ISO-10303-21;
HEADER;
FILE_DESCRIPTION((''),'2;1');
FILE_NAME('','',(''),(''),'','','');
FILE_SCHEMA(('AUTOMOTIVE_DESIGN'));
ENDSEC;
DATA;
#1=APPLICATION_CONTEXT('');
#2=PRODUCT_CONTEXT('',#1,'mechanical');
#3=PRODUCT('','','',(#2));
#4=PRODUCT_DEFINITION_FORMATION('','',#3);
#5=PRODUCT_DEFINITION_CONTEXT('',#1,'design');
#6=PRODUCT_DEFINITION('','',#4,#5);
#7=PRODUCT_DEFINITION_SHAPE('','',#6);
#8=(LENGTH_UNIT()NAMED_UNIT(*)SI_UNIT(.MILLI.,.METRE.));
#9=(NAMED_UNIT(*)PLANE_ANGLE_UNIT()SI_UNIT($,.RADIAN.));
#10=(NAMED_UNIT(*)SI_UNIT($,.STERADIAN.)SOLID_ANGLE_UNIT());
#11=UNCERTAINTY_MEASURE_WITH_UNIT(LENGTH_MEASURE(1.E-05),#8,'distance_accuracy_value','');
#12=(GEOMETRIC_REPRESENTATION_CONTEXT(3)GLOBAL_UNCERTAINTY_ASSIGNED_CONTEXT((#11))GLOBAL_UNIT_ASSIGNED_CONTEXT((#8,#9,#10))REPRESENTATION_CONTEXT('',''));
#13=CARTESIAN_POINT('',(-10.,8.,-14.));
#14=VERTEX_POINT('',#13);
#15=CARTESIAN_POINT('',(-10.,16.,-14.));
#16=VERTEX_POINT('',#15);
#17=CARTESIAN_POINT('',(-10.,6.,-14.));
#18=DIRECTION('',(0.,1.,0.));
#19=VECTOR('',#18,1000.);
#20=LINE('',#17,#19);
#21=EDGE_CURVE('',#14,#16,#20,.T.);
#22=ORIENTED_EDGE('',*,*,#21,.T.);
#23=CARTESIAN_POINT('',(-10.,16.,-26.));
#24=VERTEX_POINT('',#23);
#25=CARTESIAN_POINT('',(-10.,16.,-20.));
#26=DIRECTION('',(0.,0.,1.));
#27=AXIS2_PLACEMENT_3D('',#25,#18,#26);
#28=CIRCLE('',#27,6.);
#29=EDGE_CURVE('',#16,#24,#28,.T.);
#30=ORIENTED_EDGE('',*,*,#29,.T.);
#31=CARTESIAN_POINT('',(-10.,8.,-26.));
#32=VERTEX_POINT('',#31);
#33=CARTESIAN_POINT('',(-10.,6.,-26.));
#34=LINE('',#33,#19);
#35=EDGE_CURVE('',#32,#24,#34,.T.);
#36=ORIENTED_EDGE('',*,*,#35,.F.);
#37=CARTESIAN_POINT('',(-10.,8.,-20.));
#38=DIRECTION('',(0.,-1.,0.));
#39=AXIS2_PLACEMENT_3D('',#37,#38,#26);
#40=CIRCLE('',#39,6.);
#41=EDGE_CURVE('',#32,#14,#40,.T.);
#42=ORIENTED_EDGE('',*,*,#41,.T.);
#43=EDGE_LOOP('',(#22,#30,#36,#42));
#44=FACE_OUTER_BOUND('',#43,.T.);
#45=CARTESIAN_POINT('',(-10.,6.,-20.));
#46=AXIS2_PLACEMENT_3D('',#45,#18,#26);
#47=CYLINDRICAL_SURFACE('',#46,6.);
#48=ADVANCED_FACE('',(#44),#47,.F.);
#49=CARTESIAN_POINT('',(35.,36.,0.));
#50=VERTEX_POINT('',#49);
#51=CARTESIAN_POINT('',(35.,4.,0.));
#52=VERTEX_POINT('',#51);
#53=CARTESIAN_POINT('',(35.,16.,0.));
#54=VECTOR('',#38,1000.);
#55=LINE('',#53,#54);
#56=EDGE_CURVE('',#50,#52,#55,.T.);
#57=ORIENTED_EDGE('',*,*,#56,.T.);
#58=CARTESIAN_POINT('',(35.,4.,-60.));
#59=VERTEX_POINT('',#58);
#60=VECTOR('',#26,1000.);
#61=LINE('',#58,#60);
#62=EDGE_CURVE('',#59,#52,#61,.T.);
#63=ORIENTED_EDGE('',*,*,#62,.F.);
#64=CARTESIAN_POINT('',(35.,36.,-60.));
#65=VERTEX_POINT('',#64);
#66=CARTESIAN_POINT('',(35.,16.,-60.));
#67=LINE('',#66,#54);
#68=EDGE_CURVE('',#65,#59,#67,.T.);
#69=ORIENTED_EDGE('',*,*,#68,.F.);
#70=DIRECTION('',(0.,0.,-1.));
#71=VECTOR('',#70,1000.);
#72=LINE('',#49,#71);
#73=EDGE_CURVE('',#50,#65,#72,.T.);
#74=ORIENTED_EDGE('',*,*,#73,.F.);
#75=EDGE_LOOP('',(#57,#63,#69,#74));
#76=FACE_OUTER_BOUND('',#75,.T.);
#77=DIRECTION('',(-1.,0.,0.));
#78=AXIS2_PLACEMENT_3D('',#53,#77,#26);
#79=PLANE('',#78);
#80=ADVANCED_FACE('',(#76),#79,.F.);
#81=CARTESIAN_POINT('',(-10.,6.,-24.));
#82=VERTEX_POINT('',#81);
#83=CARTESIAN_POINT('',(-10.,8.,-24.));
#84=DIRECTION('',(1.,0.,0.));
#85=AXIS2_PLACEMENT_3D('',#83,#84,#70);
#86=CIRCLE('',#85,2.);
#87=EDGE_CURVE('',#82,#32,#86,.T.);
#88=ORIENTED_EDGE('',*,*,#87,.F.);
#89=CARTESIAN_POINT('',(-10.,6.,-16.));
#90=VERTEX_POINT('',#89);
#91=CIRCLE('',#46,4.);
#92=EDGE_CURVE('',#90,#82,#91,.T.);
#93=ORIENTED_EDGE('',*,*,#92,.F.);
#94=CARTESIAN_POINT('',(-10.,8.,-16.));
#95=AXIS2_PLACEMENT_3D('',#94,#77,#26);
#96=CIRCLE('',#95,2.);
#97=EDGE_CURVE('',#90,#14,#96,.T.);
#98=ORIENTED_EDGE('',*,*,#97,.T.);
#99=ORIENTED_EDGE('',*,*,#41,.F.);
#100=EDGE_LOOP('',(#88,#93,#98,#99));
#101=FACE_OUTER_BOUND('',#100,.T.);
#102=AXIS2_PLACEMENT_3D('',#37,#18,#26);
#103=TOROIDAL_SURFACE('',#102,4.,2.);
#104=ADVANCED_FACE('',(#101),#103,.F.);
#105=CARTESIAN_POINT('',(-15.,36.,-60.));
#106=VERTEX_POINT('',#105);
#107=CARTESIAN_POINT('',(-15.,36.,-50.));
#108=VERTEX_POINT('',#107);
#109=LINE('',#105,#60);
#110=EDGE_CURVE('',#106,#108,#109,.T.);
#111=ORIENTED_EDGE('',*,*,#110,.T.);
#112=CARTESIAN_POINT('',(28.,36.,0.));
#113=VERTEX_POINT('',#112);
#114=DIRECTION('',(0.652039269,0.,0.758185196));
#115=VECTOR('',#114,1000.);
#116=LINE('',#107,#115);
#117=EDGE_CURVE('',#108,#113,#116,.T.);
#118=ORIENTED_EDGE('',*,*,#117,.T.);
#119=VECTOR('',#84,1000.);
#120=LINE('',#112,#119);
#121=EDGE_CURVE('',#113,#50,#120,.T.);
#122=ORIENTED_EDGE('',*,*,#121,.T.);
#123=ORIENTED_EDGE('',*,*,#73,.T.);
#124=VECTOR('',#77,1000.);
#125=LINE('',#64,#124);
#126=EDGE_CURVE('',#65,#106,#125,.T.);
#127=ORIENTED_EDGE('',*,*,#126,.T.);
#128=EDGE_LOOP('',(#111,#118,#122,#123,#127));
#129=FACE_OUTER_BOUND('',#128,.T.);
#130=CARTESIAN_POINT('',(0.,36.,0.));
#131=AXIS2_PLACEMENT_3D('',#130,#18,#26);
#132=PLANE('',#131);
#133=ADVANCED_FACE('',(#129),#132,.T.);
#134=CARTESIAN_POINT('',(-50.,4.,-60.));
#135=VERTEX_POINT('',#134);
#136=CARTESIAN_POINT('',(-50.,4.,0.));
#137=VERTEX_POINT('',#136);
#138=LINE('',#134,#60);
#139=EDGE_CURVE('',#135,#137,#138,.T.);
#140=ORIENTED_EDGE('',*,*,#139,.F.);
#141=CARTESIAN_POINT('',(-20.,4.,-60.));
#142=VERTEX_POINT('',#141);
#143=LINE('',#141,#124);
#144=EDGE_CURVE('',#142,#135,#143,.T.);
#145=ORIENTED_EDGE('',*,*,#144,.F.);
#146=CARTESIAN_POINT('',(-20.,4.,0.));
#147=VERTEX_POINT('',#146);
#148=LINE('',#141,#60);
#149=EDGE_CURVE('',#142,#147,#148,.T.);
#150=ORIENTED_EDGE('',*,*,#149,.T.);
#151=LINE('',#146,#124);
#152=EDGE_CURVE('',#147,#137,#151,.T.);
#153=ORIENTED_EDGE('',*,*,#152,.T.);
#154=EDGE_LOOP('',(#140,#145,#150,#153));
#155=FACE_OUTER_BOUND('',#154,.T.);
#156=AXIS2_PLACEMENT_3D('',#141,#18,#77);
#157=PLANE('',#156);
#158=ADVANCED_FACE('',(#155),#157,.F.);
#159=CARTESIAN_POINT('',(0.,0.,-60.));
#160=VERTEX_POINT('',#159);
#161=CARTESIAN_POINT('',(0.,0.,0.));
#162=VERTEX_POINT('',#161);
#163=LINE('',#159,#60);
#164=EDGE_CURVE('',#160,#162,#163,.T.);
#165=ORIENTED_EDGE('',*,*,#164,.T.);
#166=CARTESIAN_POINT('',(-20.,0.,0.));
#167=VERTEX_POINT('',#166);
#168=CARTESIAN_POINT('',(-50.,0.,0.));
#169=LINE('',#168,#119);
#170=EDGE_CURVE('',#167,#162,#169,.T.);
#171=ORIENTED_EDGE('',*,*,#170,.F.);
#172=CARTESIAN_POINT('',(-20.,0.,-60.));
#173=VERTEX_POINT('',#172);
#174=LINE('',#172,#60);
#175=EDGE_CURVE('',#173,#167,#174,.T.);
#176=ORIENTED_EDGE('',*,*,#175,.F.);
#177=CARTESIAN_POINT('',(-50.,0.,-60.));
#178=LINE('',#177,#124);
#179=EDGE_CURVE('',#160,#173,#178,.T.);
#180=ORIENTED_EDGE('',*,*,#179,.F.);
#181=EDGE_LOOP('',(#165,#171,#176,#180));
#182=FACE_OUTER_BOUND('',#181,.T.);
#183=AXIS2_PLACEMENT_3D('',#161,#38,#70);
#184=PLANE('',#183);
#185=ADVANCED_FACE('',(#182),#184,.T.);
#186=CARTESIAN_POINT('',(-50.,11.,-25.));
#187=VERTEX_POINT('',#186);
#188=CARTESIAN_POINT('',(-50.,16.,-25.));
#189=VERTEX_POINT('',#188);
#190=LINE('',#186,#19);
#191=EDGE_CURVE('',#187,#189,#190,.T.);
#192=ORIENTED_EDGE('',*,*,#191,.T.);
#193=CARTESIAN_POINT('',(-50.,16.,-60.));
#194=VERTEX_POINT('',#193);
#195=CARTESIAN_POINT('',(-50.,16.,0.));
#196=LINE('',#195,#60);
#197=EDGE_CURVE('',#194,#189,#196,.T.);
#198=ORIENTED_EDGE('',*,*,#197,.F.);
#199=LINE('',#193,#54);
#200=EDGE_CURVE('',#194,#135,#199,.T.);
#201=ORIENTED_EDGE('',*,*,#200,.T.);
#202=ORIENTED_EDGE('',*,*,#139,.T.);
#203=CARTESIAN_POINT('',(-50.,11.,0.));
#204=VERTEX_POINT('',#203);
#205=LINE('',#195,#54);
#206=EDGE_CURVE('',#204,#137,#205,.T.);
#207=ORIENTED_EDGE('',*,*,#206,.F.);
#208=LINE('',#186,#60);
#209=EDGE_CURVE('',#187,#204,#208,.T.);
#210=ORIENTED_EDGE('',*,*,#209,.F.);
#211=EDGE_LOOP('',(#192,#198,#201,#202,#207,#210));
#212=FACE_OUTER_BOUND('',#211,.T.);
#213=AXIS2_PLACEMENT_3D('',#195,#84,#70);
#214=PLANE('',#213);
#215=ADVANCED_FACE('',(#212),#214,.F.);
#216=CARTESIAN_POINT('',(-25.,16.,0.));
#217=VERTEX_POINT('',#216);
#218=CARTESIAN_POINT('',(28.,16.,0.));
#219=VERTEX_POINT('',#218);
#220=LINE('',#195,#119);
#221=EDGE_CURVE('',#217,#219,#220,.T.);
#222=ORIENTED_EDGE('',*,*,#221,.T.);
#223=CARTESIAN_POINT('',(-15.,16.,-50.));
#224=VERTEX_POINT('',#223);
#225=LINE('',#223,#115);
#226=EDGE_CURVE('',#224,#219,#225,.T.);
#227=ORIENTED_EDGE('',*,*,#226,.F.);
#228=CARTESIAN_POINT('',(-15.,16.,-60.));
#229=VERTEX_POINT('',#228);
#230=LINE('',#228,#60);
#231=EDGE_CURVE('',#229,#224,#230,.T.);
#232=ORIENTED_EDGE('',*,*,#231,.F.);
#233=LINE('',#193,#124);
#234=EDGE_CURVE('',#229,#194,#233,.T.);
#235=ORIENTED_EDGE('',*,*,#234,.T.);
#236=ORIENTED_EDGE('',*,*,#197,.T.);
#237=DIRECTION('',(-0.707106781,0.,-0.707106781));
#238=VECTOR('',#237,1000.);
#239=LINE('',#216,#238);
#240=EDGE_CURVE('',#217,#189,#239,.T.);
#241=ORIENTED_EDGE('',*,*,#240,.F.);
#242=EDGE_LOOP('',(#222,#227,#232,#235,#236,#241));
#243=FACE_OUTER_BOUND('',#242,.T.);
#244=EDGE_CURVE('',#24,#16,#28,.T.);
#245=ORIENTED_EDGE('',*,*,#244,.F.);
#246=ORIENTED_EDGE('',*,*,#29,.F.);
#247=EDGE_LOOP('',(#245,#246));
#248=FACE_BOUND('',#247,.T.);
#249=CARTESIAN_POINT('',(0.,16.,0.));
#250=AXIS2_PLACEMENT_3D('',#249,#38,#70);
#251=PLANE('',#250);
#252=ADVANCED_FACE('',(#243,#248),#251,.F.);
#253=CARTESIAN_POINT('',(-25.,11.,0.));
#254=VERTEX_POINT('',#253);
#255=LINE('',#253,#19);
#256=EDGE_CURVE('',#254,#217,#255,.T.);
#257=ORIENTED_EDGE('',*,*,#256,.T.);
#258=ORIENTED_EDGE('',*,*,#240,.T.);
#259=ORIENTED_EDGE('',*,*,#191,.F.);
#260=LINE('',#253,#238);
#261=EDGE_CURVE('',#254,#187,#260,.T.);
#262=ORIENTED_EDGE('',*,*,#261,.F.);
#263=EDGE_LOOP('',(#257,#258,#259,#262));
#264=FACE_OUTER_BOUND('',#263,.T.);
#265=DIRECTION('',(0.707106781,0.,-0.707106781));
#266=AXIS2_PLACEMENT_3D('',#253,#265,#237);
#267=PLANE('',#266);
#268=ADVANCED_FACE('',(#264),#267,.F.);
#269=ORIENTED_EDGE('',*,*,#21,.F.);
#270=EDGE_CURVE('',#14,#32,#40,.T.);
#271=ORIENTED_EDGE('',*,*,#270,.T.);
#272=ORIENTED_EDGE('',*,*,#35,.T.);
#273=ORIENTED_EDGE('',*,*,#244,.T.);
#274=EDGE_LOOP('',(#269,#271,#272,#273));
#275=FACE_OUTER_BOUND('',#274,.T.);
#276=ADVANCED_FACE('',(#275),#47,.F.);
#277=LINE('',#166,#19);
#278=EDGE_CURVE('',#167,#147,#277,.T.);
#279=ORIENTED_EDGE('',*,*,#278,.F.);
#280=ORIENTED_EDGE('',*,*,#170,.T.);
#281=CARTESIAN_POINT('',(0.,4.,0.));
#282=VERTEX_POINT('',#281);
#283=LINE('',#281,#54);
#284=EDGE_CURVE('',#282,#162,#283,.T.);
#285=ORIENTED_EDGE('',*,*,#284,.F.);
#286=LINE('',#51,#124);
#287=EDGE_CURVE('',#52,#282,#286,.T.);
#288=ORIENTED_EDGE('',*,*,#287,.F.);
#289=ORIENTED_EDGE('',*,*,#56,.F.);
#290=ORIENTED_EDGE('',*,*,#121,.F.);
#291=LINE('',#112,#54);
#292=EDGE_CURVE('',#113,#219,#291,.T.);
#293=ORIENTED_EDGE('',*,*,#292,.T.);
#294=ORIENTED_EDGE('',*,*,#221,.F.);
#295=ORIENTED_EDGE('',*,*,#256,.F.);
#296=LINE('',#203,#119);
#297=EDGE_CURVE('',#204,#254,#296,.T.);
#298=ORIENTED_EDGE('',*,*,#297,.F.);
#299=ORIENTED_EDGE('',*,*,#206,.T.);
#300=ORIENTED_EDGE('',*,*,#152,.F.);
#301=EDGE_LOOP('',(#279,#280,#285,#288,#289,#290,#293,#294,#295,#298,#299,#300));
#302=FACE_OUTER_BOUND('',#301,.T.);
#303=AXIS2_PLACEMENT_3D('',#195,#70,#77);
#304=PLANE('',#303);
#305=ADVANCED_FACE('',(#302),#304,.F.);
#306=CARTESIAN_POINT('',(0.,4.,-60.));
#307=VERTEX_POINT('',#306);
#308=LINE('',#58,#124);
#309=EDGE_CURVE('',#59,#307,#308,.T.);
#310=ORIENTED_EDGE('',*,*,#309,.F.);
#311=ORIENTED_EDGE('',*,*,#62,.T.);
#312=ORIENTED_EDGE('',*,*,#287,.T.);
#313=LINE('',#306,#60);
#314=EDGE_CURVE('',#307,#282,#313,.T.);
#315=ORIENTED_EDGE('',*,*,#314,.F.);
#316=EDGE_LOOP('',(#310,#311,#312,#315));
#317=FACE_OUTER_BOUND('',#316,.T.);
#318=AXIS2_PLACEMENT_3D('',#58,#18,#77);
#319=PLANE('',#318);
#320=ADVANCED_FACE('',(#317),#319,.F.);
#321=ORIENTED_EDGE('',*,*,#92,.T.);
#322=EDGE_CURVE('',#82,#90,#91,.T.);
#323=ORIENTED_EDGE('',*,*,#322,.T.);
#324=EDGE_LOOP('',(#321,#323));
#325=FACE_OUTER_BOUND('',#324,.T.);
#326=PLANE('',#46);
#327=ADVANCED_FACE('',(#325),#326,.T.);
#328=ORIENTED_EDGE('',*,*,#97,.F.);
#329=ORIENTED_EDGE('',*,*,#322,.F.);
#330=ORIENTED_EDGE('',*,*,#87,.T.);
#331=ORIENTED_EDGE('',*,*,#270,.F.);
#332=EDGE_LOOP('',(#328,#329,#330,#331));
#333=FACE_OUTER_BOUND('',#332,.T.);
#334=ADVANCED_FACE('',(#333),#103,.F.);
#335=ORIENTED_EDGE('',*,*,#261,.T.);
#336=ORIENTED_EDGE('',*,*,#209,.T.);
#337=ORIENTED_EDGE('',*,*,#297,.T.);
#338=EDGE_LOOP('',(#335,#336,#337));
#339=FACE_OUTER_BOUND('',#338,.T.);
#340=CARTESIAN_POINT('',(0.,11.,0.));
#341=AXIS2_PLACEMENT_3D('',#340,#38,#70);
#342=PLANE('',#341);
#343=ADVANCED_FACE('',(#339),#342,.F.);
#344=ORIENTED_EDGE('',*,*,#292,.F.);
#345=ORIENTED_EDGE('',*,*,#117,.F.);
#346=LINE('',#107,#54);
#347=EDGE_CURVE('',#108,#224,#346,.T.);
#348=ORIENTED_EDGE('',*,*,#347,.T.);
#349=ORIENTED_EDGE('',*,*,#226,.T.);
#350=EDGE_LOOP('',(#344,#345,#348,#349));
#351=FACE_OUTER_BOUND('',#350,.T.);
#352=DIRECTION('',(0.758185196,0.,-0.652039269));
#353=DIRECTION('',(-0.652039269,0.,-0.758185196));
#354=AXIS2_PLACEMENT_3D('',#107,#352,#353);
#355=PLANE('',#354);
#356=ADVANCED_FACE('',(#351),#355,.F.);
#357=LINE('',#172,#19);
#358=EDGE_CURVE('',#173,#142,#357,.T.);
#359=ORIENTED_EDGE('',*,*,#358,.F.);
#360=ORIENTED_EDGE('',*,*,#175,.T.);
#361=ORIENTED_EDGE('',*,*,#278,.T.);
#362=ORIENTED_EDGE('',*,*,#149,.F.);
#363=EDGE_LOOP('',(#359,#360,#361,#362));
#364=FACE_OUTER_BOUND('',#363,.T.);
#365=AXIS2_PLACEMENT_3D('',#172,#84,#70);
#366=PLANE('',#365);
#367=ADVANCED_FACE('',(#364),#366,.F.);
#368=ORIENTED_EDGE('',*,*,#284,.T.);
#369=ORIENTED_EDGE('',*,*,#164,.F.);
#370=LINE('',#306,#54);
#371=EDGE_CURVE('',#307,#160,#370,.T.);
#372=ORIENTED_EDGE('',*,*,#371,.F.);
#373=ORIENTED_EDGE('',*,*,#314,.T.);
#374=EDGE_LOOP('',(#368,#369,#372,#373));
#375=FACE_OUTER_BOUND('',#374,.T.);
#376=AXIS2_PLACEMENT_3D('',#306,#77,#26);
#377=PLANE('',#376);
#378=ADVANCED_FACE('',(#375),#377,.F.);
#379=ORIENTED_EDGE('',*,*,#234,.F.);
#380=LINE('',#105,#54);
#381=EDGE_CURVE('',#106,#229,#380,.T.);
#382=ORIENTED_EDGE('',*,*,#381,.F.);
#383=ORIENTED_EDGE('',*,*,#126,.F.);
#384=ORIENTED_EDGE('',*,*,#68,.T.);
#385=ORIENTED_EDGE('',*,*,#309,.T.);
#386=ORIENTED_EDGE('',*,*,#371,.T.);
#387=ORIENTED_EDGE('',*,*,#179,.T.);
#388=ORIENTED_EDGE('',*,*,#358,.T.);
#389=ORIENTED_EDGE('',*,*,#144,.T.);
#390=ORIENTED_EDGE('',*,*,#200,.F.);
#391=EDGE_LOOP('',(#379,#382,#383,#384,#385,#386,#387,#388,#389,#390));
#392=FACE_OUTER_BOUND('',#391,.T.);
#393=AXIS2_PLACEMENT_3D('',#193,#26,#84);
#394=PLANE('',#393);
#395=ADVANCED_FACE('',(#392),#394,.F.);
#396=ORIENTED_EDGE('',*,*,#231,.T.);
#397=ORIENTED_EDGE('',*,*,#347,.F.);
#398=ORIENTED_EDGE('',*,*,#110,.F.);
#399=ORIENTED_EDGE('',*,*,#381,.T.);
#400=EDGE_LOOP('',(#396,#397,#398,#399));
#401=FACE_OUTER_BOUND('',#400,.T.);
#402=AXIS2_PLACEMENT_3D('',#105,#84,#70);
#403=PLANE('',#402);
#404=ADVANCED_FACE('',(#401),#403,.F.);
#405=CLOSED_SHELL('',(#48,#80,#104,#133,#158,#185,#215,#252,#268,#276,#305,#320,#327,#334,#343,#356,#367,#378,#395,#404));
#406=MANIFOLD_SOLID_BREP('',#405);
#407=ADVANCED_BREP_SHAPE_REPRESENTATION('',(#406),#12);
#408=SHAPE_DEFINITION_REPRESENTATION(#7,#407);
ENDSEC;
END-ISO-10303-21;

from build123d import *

# Parameters (mm, degrees)
BASE_BLOCK_SKETCH_W        = 85
BASE_BLOCK_SKETCH_H        = 60
BASE_BLOCK_85X60X16_DEPTH  = 16
UNDERSIDE_STEP_SKETCH_W    = 30
UNDERSIDE_STEP_SKETCH_H    = 4
UNDERSIDE_STEP_CUT_DEPTH   = 80.724525712
RELIEF_CUT_SKETCH_W        = 35
RELIEF_CUT_SKETCH_H        = 4
RELIEF_CUT_4MM_DEPTH       = 80.724525712
RAISED_BLOCK_20MM_DEPTH    = 20
TRIANGULAR_NOTCH_CUT_DEPTH = 5
HOLE_12_SKETCH_R           = 6
HOLE_12X10_DEPTH           = 10
FILLET_R2_R                = 2


with BuildPart() as part:
    # Base Block Sketch → Base Block 85x60x16 (new body)
    with BuildSketch(Plane(origin=(0, 0, 0), x_dir=(1, 0, 0), z_dir=(0, 1, 0))):
        with Locations((-7.5, 30)):
            Rectangle(BASE_BLOCK_SKETCH_W, BASE_BLOCK_SKETCH_H)
    extrude(amount=BASE_BLOCK_85X60X16_DEPTH)

    # Underside Step Sketch → Underside Step Cut (cut, through all)
    with BuildSketch(Plane.XY):
        with Locations((-35, 2)):
            Rectangle(UNDERSIDE_STEP_SKETCH_W, UNDERSIDE_STEP_SKETCH_H)
    extrude(amount=-UNDERSIDE_STEP_CUT_DEPTH, mode=Mode.SUBTRACT)

    # Relief Cut Sketch → Relief Cut 4mm (cut, through all)
    with BuildSketch(Plane.XY):
        with Locations((17.5, 2)):
            Rectangle(RELIEF_CUT_SKETCH_W, RELIEF_CUT_SKETCH_H)
    extrude(amount=-RELIEF_CUT_4MM_DEPTH, mode=Mode.SUBTRACT)

    # Raised Block Sketch → Raised Block 20mm (add)
    with BuildSketch(Plane(origin=(0, 16, 0), x_dir=(1, 0, 0), z_dir=(0, 1, 0))):
        Polygon((35, 60), (-15, 60), (-15, 50), (28, 0), (35, 0), align=None)
    extrude(amount=RAISED_BLOCK_20MM_DEPTH)

    # Notch Sketch → Triangular Notch Cut (cut)
    with BuildSketch(Plane(origin=(0, 16, 0), x_dir=(1, 0, 0), z_dir=(0, 1, 0))):
        Polygon((-25, 0), (-50, 25), (-50, 0), align=None)
    extrude(amount=-TRIANGULAR_NOTCH_CUT_DEPTH, mode=Mode.SUBTRACT)

    # Hole Ø12 Sketch → Hole Ø12x10 (cut)
    with BuildSketch(Plane(origin=(0, 16, 0), x_dir=(1, 0, 0), z_dir=(0, 1, 0))):
        with Locations(Location((-10, 20, 0), (0, 0, 270))):
            Circle(HOLE_12_SKETCH_R)
    extrude(amount=-HOLE_12X10_DEPTH, mode=Mode.SUBTRACT)

    # Fillet R2
    fillet_r2_edges = [part.edges().sort_by_distance(p)[0] for p in [
        (-10, 6, -26),
    ]]
    fillet(fillet_r2_edges, radius=FILLET_R2_R)


solid = part.part
